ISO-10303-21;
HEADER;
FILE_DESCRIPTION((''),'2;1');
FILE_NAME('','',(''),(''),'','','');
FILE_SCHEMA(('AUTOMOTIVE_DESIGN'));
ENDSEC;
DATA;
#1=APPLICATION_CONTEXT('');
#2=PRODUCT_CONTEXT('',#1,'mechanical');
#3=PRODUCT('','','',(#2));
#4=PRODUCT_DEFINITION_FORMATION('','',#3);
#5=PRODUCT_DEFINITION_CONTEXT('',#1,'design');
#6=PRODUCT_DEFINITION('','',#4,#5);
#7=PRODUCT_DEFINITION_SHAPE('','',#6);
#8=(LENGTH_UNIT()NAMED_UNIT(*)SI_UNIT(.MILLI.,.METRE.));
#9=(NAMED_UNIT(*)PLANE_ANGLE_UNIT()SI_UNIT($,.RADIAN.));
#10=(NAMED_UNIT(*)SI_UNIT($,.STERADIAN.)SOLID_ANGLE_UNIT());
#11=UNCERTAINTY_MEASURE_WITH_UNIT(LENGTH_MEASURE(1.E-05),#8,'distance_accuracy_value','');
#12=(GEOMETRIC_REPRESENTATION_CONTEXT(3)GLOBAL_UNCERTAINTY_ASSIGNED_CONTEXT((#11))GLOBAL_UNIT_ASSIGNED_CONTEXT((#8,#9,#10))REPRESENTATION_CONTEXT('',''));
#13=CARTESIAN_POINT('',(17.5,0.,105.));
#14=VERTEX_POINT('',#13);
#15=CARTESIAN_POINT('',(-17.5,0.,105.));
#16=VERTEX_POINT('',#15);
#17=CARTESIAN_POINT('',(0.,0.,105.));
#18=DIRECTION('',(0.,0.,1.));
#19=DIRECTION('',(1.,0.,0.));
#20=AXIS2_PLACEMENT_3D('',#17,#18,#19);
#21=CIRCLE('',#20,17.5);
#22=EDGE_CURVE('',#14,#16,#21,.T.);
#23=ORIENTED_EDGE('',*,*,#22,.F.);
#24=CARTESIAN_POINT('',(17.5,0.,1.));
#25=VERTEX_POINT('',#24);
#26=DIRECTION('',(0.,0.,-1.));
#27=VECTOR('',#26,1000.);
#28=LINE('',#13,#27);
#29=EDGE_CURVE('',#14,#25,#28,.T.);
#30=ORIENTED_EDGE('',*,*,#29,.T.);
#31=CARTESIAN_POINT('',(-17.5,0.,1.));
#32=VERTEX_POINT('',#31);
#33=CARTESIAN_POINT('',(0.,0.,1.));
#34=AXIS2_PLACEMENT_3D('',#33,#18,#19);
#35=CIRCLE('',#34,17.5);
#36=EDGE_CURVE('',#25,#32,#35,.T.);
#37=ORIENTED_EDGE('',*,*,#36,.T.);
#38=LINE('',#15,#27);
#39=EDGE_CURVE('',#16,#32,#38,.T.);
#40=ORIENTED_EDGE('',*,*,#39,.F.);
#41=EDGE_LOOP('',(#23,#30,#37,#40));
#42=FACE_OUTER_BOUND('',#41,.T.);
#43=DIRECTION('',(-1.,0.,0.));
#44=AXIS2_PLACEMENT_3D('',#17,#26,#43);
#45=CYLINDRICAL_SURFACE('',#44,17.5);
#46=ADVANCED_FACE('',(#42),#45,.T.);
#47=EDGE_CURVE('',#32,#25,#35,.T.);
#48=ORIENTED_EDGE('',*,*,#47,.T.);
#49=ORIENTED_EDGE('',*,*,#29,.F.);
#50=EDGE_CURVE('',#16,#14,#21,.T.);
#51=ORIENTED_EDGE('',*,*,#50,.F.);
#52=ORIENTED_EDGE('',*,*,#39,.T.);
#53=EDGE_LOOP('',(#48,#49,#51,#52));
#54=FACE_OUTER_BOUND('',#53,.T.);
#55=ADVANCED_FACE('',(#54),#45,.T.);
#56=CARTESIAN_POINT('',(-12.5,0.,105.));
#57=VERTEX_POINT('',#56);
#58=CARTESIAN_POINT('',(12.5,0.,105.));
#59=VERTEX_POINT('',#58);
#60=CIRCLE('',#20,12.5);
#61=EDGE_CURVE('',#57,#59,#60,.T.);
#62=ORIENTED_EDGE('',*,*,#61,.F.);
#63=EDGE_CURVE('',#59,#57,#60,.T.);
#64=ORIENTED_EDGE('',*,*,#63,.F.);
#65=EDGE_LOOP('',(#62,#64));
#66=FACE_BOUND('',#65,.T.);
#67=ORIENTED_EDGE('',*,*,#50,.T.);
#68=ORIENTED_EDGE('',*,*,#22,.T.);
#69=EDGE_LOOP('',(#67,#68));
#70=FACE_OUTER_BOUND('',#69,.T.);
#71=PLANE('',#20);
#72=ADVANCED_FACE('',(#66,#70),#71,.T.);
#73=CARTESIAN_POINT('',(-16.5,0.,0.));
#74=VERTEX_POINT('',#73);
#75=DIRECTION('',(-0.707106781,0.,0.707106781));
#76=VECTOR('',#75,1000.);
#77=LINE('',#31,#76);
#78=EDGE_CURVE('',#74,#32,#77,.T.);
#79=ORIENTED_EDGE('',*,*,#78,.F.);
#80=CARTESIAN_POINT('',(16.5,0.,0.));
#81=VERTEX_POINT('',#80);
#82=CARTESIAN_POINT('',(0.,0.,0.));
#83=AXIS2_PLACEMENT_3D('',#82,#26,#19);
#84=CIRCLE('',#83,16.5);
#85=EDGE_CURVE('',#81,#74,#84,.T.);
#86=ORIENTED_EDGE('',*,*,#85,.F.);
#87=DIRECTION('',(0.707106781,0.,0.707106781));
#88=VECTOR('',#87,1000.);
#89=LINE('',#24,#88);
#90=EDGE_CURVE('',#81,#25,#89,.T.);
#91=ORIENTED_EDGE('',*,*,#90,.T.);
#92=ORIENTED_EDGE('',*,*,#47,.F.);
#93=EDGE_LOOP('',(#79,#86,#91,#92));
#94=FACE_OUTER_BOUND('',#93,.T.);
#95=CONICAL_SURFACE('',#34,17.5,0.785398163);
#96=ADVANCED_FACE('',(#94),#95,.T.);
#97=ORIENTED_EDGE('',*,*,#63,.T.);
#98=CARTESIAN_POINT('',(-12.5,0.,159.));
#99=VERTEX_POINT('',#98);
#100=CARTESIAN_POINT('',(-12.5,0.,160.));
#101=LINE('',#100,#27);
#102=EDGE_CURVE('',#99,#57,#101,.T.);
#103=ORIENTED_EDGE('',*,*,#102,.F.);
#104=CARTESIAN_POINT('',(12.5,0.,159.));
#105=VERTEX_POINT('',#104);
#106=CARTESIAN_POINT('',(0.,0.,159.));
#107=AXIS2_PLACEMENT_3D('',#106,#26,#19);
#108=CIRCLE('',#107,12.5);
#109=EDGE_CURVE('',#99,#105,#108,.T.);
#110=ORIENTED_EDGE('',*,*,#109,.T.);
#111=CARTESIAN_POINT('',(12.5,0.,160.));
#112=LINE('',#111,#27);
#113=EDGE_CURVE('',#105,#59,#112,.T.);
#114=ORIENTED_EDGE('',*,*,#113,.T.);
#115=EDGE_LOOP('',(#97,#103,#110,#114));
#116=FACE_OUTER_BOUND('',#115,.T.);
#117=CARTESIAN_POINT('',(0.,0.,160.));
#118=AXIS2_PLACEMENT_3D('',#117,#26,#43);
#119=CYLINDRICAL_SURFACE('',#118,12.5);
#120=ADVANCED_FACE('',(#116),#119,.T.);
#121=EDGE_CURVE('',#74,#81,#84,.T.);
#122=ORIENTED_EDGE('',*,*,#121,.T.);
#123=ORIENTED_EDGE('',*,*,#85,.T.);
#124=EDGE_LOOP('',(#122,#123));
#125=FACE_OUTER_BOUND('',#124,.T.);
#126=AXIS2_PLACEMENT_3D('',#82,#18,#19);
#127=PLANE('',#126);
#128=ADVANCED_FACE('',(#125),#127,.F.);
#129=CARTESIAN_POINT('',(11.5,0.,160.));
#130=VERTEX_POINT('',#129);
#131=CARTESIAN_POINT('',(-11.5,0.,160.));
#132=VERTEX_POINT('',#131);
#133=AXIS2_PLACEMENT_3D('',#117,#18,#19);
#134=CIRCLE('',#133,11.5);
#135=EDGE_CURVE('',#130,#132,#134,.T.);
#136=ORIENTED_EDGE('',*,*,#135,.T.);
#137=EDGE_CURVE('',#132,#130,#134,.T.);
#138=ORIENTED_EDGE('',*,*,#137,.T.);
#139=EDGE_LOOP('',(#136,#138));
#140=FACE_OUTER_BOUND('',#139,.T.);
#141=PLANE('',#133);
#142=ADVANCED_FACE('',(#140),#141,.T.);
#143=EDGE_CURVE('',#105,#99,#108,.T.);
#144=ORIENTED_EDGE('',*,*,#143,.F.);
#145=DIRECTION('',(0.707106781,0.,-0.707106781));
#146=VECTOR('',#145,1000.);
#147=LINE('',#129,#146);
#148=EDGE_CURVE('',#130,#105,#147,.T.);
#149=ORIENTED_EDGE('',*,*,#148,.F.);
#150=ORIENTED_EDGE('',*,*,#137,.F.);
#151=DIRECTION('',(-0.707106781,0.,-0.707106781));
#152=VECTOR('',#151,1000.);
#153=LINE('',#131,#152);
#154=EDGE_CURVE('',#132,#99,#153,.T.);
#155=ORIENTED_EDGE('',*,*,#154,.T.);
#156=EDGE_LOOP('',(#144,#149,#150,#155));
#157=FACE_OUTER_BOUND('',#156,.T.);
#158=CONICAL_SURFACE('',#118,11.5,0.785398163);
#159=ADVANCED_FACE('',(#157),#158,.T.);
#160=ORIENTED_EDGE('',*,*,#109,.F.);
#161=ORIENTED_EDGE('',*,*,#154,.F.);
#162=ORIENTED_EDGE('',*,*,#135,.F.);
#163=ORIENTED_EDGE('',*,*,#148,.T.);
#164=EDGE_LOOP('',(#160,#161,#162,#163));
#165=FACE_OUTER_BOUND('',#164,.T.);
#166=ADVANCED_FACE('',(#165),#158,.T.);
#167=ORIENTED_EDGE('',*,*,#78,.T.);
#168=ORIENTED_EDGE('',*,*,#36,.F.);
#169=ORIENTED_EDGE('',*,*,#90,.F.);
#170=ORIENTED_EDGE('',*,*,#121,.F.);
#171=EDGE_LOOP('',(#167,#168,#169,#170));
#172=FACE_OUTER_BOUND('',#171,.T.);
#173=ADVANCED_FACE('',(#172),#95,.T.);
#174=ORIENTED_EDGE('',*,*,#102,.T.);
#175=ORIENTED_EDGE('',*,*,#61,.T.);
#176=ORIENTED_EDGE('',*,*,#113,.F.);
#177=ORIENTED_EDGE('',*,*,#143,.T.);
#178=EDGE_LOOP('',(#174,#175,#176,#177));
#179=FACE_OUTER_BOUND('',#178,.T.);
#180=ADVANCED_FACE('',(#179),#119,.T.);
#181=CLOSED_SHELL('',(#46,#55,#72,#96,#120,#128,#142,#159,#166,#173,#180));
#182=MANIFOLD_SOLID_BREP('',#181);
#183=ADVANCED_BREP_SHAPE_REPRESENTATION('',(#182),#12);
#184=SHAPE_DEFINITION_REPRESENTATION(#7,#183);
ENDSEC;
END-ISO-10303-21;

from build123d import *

# Parameters (mm, degrees)
SKETCH1_R           = 17.5
BOSS_EXTRUDE1_DEPTH = 105
SKETCH2_R           = 12.5
BOSS_EXTRUDE2_DEPTH = 55
CHAMFER1_SIZE       = 1


with BuildPart() as part:
    # Sketch1 → Boss-Extrude1 (new body)
    with BuildSketch(Plane.XY):
        Circle(SKETCH1_R)
    extrude(amount=BOSS_EXTRUDE1_DEPTH)

    # Sketch2 → Boss-Extrude2 (add)
    with BuildSketch(Plane.XY.offset(105)):
        Circle(SKETCH2_R)
    extrude(amount=BOSS_EXTRUDE2_DEPTH)

    # Chamfer1
    chamfer1_edges = [part.edges().sort_by_distance(p)[0] for p in [
        (-17.5, 0, 0),
        (-12.5, 0, 160),
    ]]
    chamfer(chamfer1_edges, length=CHAMFER1_SIZE)


solid = part.part
